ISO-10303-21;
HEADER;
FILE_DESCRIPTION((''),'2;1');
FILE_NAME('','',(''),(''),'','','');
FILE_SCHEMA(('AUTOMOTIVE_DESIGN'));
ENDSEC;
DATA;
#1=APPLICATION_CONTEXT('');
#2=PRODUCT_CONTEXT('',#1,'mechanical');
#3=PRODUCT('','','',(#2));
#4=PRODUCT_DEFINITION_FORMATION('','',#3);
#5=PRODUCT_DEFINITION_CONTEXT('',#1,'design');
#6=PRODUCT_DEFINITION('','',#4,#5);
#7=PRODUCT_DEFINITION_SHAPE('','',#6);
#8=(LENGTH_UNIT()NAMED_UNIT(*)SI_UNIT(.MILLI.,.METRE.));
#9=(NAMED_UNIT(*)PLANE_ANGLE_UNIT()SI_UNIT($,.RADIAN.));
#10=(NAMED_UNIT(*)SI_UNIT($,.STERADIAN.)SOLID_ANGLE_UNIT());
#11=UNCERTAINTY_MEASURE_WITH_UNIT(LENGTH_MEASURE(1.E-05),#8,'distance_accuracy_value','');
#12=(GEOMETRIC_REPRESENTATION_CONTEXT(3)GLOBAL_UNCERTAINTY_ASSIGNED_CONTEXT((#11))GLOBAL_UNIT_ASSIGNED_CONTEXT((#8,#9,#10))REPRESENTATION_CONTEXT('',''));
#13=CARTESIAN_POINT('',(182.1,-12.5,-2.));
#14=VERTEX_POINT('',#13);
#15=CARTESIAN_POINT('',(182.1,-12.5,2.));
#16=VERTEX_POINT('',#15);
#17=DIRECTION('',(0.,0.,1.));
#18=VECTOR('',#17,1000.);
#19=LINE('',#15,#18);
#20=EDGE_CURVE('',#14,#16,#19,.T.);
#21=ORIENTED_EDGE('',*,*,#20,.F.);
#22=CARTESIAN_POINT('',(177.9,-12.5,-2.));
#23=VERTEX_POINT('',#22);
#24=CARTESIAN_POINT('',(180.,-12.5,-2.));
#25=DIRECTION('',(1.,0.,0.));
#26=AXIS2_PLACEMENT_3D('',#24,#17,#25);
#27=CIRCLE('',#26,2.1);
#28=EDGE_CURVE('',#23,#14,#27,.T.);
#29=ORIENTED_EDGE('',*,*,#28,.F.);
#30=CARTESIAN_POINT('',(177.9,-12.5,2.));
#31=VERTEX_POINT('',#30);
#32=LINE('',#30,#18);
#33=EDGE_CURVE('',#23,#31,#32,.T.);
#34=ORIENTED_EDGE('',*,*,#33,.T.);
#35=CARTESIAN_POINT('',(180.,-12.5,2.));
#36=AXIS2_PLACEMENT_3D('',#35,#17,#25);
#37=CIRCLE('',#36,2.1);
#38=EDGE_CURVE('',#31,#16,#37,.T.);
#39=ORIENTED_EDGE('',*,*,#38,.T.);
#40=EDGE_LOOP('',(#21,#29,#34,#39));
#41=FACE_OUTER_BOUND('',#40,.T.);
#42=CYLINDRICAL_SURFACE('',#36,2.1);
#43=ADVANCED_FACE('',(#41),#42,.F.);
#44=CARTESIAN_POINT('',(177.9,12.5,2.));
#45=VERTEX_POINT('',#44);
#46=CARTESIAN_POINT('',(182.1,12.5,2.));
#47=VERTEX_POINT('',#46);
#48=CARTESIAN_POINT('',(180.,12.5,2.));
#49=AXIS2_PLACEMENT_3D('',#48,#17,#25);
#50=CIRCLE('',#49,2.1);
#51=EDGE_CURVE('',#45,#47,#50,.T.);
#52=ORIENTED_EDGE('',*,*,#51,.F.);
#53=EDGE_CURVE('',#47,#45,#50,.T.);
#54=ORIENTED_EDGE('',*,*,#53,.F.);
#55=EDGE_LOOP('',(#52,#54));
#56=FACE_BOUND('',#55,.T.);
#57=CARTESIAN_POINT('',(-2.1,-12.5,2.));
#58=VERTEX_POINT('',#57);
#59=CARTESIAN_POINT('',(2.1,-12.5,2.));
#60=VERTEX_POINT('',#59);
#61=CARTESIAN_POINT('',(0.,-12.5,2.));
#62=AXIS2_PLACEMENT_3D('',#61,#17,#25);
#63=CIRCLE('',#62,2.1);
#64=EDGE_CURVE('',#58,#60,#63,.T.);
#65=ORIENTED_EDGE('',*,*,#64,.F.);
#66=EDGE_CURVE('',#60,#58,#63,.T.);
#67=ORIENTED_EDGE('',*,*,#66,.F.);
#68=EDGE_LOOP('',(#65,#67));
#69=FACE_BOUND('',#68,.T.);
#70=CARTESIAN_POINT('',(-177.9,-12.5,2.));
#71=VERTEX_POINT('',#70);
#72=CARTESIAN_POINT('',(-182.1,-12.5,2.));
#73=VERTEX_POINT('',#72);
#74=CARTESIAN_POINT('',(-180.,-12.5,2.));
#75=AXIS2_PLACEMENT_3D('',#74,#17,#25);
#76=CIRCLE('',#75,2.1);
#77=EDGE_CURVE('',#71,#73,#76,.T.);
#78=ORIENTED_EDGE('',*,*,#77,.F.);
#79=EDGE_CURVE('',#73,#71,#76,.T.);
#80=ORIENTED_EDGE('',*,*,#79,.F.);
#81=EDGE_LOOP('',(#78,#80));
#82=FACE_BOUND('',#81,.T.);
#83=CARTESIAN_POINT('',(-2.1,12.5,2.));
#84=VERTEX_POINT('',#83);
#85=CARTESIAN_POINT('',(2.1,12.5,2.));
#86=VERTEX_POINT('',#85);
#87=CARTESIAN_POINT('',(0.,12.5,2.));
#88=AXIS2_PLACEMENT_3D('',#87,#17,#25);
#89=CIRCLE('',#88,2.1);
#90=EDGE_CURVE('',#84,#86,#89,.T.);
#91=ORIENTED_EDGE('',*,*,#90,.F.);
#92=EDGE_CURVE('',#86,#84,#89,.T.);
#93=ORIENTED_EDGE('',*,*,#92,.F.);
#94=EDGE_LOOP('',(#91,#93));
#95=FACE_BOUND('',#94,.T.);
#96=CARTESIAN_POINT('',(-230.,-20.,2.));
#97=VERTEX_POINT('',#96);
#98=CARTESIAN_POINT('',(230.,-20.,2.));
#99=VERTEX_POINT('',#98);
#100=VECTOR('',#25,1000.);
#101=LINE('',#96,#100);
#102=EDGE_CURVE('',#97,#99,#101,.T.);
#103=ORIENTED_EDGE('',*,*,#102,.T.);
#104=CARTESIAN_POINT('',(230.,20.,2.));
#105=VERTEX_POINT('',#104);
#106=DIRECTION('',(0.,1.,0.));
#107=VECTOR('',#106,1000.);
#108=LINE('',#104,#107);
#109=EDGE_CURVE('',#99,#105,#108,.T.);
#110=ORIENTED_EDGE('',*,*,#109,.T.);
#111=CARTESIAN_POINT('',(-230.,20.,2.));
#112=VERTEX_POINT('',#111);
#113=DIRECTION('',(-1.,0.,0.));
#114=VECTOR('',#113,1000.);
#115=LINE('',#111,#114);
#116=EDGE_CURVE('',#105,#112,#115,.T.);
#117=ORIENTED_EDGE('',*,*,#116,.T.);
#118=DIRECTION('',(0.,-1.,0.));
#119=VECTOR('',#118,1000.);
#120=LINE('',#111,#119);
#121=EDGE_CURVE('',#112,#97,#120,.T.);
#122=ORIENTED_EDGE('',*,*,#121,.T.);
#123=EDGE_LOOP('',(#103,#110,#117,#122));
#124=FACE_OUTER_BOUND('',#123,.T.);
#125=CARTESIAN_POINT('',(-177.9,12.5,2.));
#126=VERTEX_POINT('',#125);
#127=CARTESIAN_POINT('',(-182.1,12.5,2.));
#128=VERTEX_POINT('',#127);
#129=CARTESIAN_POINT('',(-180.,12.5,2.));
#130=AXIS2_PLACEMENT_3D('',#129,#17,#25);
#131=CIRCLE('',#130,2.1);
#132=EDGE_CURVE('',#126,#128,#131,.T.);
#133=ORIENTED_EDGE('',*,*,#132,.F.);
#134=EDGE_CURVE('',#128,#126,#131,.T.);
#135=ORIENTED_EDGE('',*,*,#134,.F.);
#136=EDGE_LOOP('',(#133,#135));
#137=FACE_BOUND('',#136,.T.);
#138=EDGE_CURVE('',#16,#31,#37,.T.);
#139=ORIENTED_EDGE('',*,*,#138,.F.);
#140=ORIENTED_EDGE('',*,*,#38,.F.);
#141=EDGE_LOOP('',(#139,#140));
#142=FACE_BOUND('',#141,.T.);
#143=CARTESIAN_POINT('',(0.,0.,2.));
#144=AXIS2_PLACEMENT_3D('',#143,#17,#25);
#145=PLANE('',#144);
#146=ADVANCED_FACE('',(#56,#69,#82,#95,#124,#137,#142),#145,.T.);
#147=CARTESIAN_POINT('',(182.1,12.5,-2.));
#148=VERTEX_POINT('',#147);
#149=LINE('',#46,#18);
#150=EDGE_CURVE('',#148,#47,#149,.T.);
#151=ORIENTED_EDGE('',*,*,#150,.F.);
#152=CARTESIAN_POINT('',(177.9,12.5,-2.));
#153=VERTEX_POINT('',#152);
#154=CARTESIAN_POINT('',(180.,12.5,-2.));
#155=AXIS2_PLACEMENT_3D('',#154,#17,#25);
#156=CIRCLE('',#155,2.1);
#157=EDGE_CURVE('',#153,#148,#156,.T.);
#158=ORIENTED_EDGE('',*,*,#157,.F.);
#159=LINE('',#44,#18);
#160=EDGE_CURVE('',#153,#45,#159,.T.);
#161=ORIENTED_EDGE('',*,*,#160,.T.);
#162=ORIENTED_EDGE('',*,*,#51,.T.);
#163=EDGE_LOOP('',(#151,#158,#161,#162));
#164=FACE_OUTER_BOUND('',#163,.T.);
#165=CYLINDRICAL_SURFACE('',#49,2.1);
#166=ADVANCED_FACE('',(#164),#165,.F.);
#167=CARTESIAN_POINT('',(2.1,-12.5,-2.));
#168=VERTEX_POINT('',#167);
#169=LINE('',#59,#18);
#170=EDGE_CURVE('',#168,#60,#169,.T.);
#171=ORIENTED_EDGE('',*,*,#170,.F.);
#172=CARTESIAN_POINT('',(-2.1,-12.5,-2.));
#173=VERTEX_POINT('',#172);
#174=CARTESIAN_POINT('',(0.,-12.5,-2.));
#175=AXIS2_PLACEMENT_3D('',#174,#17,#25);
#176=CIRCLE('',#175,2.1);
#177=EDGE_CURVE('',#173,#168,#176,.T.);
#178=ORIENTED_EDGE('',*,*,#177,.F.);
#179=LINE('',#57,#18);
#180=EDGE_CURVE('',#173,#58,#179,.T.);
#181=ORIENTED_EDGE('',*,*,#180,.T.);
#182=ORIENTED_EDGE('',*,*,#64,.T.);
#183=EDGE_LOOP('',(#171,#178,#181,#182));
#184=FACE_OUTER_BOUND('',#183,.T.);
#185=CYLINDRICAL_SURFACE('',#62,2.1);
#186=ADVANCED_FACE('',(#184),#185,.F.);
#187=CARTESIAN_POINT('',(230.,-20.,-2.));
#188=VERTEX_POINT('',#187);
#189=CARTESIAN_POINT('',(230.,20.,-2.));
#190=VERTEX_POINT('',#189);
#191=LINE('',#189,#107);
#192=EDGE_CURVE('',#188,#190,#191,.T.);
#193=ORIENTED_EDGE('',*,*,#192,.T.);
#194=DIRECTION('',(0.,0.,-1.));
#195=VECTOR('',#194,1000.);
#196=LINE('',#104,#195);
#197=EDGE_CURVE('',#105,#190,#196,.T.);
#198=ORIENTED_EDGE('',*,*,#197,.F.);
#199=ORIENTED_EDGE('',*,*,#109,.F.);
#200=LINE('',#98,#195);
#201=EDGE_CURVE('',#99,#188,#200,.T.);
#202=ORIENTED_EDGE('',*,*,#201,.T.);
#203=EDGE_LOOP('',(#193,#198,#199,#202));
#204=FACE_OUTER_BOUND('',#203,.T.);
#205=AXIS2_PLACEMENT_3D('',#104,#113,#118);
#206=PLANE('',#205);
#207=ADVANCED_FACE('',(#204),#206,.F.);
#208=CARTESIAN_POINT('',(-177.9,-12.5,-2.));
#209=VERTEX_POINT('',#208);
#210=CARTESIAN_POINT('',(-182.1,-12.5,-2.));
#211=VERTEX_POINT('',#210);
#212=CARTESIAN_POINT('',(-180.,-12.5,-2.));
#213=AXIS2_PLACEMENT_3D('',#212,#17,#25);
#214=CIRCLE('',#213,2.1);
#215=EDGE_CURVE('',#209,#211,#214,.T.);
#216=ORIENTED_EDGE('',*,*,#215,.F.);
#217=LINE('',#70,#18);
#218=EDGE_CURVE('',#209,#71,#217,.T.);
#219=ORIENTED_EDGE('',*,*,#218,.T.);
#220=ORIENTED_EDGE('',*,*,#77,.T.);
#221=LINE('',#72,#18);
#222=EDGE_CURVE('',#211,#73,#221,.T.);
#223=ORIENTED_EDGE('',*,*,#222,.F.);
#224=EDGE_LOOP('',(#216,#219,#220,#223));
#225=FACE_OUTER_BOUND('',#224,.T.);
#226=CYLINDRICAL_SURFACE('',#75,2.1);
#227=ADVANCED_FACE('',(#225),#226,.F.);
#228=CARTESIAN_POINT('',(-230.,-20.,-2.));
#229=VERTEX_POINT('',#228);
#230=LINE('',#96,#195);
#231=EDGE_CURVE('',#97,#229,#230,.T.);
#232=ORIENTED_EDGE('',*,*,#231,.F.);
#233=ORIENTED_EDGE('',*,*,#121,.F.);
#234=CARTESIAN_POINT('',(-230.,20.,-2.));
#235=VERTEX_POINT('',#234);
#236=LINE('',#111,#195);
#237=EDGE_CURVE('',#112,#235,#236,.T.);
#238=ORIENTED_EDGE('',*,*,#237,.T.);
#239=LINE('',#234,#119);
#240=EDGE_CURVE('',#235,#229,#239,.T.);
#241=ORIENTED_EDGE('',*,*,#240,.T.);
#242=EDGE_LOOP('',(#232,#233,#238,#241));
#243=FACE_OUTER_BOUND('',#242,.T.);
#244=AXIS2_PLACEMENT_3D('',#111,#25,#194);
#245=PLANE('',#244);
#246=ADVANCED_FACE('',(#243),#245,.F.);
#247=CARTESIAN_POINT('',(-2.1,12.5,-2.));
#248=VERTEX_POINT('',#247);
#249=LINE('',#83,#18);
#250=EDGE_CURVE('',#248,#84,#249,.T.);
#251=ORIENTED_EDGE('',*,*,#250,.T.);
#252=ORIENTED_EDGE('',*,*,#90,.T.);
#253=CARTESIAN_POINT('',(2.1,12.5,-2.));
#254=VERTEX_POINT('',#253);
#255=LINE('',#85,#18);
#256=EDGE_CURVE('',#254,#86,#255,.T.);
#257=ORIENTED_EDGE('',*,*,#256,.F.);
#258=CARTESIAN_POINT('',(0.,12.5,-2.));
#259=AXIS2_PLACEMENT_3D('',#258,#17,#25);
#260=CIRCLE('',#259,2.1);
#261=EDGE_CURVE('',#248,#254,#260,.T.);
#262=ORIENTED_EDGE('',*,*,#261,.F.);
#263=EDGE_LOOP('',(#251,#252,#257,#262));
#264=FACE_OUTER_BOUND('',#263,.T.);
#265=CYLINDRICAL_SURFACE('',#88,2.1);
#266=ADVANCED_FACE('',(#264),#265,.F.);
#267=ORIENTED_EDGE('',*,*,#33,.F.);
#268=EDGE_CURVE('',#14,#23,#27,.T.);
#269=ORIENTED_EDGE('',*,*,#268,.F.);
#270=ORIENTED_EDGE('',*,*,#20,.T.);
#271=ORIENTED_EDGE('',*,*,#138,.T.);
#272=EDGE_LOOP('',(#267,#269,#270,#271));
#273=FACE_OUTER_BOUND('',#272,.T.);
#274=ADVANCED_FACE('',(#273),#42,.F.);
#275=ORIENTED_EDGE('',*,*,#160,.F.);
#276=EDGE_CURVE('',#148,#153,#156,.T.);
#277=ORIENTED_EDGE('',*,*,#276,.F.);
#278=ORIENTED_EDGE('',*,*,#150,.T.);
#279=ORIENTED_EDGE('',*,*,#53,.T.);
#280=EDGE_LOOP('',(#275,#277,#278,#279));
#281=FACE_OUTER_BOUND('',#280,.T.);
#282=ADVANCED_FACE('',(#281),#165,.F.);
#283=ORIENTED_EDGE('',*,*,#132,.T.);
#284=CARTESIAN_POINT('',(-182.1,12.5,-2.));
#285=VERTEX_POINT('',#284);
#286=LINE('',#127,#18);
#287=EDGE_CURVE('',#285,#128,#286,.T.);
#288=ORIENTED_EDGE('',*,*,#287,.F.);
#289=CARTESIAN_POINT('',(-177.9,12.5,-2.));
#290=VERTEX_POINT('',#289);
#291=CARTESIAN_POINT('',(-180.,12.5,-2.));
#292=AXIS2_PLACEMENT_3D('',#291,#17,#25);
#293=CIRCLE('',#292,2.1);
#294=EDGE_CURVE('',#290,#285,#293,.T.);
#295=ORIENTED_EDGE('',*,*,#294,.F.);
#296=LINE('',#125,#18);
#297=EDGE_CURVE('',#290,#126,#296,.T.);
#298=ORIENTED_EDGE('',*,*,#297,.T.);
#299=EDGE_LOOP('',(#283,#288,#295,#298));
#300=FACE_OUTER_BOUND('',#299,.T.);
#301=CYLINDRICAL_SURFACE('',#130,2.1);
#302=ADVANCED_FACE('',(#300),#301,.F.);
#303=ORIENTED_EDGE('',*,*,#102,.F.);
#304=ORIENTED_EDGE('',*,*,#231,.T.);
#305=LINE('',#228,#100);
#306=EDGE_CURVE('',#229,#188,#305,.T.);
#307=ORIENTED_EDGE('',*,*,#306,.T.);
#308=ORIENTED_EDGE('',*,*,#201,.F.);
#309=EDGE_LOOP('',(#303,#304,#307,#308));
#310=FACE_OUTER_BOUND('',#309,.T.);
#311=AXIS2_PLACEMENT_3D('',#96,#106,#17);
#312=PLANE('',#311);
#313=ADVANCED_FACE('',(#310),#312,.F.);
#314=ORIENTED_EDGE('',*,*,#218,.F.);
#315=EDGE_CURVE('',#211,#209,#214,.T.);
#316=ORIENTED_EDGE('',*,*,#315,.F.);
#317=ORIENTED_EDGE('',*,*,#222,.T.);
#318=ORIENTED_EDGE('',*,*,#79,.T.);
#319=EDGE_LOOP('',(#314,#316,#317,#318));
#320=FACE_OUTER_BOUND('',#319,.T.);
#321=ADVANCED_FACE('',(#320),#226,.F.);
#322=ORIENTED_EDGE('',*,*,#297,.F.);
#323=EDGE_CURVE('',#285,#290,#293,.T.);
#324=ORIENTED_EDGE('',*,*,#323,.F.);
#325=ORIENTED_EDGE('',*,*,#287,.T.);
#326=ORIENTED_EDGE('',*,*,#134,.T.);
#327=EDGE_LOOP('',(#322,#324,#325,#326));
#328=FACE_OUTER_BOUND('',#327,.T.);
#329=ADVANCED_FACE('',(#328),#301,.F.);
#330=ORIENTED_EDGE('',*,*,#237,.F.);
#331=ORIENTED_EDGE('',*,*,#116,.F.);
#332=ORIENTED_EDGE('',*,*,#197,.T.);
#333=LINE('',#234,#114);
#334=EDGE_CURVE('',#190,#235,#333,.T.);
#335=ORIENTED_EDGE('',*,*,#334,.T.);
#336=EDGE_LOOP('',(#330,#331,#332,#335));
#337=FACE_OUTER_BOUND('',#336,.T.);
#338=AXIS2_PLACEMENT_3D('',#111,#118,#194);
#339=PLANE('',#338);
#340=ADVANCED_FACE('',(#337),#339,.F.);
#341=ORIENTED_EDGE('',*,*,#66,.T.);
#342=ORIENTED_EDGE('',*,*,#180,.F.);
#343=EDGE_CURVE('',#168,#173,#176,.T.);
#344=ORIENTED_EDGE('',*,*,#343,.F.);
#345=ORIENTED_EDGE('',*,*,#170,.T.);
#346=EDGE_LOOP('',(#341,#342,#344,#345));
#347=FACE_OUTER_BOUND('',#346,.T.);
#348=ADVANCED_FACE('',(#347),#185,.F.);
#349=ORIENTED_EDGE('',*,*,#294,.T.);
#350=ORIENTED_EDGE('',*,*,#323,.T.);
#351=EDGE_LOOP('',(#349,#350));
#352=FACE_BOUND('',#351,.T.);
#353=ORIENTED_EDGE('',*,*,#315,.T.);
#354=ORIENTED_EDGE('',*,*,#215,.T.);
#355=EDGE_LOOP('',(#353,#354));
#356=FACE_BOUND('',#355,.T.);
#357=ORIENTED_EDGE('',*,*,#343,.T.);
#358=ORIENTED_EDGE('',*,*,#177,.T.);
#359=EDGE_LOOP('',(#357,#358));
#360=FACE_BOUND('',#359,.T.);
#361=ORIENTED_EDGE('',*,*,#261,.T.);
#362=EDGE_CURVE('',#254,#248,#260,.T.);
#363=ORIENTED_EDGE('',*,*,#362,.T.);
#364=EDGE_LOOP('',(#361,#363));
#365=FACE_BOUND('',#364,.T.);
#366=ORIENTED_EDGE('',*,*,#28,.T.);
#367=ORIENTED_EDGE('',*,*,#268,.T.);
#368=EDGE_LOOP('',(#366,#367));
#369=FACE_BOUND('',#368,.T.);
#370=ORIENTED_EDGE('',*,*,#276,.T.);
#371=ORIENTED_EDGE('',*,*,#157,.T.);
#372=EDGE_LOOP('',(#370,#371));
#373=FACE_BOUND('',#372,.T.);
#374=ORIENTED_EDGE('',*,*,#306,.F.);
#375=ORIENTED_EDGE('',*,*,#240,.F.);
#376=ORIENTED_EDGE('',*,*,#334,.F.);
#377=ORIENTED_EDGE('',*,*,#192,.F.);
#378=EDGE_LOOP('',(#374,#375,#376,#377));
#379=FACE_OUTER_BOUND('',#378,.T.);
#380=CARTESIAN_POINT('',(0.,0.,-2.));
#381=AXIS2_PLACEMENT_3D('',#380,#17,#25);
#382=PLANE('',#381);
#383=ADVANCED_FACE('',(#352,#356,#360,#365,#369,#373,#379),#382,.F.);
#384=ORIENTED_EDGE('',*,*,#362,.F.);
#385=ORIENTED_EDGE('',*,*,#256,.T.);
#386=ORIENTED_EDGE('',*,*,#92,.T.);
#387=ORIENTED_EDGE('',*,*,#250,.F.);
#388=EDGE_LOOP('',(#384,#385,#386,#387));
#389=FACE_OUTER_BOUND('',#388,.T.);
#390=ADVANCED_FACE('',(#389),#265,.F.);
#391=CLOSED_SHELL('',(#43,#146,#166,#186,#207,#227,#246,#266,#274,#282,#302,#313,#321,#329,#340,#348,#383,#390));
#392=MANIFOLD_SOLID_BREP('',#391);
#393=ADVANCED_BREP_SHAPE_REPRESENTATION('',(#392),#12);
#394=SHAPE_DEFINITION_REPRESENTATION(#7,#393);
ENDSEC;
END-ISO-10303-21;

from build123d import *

# Parameters (mm, degrees)
SKETCH_1_W             = 460
SKETCH_1_H             = 40
EXTRUDE_1_DEPTH        = 2
HOLE_WIZARD_M5_1_D     = 4.2
HOLE_WIZARD_M5_1_DEPTH = 14
HOLE_WIZARD_M5_1_TIP   = 1.2618073


with BuildPart() as part:
    # 草图1 → 凸台-拉伸1 (new, symmetric)
    with BuildSketch(Plane.XY):
        Rectangle(SKETCH_1_W, SKETCH_1_H)
    extrude(amount=EXTRUDE_1_DEPTH, both=True)

    # M5 螺纹孔1
    with Locations(Plane.XY.offset(2)):
        with Locations((-180, 12.5), (-180, -12.5), (0, 12.5), (0, -12.5), (180, 12.5), (180, -12.5)):
            Hole(HOLE_WIZARD_M5_1_D / 2, depth=HOLE_WIZARD_M5_1_DEPTH)
            with Locations((0, 0, -(HOLE_WIZARD_M5_1_DEPTH + HOLE_WIZARD_M5_1_TIP / 2))):  # 118° drill point
                Cone(0, HOLE_WIZARD_M5_1_D / 2, HOLE_WIZARD_M5_1_TIP, mode=Mode.SUBTRACT)


solid = part.part
